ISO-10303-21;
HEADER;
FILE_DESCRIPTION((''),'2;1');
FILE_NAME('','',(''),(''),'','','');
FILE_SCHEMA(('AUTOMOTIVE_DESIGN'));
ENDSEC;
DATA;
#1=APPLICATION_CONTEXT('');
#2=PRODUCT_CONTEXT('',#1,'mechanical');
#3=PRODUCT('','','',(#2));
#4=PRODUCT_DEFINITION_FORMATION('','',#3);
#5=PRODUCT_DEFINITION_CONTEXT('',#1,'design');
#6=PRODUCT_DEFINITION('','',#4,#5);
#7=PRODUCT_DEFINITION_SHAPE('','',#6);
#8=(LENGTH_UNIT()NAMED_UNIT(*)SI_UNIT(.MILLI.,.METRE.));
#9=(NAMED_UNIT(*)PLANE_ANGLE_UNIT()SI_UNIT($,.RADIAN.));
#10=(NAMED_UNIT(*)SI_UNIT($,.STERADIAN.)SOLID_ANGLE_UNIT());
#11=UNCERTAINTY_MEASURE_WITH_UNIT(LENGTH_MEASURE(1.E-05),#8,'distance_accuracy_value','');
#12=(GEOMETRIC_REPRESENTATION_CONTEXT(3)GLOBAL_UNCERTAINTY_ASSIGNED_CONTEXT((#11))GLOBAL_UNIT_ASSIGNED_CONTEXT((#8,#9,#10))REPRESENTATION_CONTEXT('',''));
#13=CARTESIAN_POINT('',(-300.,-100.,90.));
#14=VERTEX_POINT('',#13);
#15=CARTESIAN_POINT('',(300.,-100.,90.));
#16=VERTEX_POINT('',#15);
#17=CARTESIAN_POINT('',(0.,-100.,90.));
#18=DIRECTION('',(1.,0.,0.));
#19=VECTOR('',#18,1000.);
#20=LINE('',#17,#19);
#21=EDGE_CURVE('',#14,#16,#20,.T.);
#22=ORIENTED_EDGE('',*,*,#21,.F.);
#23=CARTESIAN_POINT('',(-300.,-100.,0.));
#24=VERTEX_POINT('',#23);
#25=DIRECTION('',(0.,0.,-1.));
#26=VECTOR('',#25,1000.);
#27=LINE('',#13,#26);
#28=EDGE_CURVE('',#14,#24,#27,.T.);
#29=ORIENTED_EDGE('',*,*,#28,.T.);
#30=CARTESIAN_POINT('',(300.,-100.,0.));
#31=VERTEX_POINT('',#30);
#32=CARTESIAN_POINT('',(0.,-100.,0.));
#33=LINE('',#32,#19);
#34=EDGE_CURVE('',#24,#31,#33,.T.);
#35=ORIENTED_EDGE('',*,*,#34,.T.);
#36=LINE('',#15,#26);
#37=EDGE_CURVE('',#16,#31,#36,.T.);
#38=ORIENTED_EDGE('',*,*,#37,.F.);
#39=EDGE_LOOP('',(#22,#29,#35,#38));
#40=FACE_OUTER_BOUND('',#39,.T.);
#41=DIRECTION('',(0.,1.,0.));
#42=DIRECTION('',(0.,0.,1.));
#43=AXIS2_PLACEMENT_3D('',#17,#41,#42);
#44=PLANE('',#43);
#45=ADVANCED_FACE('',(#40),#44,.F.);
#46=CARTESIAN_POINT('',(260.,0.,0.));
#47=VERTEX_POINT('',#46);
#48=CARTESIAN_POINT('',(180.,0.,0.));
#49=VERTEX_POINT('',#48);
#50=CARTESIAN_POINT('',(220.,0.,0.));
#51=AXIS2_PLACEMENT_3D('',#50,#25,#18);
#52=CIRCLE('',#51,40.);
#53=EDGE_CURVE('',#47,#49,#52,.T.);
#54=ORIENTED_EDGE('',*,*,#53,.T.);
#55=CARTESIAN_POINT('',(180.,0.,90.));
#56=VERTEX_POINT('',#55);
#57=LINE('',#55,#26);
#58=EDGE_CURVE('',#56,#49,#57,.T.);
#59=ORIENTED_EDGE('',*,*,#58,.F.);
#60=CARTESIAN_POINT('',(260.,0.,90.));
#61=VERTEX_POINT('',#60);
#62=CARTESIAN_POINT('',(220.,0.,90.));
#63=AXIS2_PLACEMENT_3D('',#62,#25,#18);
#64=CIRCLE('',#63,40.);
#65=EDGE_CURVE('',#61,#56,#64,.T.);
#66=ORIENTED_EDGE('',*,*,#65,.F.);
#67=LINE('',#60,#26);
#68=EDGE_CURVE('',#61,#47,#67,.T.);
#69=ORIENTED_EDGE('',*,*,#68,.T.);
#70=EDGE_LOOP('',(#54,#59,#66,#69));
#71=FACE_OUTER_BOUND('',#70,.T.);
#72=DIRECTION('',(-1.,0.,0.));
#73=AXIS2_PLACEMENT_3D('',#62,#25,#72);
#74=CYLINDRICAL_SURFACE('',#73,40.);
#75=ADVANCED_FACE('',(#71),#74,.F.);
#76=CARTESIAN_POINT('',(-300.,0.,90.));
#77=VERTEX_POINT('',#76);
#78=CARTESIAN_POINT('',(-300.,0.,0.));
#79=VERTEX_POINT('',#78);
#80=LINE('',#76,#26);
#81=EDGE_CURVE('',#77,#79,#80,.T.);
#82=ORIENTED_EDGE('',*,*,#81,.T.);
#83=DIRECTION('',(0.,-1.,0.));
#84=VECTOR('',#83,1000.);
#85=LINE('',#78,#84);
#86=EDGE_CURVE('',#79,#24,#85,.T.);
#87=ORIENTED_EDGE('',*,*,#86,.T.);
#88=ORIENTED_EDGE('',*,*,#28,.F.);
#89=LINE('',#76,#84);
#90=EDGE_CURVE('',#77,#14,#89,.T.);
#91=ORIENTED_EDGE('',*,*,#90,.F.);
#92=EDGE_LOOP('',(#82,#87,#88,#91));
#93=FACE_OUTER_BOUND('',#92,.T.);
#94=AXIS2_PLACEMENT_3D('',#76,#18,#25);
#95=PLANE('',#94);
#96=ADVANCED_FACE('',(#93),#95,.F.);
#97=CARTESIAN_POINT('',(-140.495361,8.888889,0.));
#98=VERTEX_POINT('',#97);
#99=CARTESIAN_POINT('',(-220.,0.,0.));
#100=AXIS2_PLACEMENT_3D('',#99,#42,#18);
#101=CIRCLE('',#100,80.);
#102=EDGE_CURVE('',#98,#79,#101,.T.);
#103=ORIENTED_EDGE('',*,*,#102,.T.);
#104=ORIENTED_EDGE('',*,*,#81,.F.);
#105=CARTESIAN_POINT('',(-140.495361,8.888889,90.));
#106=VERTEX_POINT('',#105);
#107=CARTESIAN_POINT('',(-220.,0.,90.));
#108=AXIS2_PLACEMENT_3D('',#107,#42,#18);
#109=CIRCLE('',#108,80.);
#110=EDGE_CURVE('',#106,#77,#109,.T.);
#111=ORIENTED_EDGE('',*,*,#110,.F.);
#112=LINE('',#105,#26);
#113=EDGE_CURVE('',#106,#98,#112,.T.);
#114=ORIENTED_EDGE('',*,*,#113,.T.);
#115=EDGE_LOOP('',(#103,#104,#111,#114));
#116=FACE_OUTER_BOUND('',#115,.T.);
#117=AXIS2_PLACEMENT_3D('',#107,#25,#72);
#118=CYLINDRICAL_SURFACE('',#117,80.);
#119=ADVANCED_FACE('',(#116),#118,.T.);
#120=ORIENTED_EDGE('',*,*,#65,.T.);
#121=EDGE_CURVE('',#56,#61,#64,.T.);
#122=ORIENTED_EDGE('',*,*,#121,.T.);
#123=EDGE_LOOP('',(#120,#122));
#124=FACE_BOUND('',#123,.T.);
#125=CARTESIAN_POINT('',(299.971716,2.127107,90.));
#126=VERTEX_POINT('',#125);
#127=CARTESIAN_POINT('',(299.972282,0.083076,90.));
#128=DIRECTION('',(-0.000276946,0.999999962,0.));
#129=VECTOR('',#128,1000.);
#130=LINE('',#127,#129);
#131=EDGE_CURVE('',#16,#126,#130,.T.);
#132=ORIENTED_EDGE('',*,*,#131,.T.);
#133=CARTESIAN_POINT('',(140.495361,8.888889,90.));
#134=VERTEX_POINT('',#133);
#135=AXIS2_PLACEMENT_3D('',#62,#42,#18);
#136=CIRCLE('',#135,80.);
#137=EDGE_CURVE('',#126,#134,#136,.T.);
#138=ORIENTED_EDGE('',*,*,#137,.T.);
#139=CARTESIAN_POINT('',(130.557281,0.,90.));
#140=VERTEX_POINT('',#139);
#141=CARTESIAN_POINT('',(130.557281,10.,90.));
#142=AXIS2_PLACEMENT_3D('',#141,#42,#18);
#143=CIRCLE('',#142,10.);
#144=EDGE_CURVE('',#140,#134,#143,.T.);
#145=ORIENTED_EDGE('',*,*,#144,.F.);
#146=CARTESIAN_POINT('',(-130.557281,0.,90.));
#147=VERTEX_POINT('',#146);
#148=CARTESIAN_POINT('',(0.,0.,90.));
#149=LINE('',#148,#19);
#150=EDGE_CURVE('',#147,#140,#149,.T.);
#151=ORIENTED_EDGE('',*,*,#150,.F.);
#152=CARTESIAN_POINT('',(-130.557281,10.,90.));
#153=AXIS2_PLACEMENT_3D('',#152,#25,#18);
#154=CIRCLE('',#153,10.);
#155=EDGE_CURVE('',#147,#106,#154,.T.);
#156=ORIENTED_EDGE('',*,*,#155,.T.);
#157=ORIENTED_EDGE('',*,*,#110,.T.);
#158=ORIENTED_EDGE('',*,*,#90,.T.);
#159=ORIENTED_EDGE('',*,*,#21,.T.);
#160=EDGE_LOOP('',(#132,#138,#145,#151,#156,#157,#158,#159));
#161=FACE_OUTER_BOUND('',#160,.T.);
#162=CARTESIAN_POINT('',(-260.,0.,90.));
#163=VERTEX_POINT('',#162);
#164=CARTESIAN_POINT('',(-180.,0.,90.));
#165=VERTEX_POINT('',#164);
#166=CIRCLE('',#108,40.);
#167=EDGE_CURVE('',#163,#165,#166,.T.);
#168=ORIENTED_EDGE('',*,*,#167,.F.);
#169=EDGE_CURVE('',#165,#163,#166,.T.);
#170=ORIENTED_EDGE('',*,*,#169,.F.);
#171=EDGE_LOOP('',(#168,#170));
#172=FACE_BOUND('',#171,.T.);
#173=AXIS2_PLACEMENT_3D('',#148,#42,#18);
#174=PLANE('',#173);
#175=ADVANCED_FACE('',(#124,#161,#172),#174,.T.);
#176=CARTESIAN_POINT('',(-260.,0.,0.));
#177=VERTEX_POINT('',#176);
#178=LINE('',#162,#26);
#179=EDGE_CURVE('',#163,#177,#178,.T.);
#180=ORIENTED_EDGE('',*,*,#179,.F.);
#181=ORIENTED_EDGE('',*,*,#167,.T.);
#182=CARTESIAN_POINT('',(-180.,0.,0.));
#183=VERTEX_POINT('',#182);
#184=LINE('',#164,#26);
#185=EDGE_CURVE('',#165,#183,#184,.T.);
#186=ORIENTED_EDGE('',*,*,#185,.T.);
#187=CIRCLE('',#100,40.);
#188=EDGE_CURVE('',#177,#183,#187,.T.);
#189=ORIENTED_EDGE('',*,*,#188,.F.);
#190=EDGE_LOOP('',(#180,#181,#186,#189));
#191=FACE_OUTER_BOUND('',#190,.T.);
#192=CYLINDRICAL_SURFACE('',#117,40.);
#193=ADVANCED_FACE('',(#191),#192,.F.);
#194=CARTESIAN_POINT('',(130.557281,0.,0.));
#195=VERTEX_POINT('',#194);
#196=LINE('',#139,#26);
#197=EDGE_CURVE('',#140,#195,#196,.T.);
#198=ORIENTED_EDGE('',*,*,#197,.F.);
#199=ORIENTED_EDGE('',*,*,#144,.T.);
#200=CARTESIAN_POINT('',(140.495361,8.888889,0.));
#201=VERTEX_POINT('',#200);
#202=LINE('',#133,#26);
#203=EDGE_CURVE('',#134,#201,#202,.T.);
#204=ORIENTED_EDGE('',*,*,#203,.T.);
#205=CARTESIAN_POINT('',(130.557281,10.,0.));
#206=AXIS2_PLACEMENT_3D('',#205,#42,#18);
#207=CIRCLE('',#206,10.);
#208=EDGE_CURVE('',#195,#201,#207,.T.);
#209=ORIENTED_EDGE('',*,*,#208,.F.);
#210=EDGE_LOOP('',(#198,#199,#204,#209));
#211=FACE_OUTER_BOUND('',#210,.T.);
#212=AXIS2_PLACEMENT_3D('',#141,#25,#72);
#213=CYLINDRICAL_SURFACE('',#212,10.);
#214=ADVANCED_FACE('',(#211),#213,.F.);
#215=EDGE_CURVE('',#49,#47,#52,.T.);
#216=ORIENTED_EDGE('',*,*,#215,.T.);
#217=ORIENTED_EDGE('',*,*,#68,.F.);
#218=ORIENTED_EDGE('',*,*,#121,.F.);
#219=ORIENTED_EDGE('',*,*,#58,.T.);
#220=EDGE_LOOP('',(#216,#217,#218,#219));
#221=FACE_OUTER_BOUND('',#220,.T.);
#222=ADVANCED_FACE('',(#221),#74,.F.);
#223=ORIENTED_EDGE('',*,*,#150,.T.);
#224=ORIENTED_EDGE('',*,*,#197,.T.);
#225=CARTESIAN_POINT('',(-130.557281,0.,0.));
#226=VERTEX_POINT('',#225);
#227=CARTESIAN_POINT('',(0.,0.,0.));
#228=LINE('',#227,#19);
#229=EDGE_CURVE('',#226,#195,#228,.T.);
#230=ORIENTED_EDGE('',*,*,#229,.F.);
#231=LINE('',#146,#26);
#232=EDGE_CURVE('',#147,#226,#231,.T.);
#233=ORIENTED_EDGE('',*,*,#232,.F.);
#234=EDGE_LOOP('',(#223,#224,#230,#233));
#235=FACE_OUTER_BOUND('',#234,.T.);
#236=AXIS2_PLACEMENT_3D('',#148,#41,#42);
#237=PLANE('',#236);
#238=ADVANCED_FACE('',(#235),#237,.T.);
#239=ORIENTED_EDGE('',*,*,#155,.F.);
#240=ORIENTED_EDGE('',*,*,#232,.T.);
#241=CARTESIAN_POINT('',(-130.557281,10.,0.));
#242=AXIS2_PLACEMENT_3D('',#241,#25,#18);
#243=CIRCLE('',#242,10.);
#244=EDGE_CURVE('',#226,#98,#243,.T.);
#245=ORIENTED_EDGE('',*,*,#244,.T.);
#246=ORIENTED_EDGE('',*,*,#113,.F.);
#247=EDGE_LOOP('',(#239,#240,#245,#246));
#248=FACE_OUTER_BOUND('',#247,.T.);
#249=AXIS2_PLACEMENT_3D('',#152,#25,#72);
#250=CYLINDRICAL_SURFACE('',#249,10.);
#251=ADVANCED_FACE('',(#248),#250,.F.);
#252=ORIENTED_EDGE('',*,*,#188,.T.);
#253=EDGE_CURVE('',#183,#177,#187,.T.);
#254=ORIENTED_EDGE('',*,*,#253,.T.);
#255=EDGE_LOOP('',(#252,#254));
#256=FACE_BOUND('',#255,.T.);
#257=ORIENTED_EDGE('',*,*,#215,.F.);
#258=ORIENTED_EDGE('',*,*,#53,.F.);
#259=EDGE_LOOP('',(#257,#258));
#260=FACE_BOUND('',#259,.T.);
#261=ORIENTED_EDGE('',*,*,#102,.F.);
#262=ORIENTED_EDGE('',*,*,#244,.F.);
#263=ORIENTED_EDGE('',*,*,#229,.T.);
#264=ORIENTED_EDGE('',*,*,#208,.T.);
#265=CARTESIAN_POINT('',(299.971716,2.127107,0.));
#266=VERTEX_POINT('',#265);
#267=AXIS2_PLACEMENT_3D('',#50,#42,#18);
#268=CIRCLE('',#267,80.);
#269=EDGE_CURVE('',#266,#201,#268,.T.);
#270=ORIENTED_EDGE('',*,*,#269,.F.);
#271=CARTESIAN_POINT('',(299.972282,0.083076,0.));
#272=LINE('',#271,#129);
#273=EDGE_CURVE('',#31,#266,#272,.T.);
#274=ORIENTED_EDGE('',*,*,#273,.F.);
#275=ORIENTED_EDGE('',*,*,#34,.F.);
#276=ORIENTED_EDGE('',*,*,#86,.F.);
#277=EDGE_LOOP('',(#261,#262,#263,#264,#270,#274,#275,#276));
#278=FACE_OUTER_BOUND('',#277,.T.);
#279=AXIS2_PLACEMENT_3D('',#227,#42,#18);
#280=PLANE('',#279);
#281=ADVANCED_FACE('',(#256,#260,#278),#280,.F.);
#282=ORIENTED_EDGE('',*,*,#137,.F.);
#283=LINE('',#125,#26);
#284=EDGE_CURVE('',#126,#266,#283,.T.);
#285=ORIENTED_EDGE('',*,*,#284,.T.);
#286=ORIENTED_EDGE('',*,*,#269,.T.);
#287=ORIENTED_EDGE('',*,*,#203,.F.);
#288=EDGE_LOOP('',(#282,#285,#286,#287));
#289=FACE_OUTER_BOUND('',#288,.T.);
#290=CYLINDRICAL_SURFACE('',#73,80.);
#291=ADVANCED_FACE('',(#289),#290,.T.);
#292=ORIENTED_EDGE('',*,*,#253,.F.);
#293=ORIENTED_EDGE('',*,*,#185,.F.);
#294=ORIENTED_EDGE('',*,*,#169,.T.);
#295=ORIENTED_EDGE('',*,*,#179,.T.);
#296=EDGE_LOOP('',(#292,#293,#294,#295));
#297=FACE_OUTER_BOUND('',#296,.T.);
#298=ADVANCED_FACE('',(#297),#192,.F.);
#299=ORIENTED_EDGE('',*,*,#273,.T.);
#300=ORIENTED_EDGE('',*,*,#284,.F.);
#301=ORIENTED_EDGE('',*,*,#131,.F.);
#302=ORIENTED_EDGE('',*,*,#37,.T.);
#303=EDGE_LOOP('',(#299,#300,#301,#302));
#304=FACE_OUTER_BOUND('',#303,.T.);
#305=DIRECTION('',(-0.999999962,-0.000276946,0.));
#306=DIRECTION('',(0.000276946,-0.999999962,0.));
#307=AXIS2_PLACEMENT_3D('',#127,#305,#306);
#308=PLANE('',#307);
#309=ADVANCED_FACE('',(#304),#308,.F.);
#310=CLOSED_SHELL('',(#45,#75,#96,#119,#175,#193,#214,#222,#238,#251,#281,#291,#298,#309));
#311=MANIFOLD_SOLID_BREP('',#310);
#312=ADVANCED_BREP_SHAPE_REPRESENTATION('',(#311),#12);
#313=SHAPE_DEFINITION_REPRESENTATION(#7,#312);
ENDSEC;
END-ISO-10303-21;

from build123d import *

# Parameters (mm, degrees)
SKETCH1_R           = 40
BOSS_EXTRUDE2_DEPTH = 90


with BuildPart() as part:
    # Sketch1 → Boss-Extrude2 (new body)
    with BuildSketch(Plane.XY):
        with BuildLine():
            ThreePointArc((-140.4953608, 8.888888889), (-224.451340472, 79.876063799), (-300, 0))
            Line((-300, 0), (-300, -100))
            Line((-300, -100), (300, -100))
            Line((300, -100), (299.972882257, -2.08281146))
            Line((299.972882257, -2.08281146), (299.971716338, 2.127107427))
            ThreePointArc((299.971716338, 2.127107427), (223.388947093, 79.928186753), (140.4953608, 8.888888889))
            ThreePointArc((140.4953608, 8.888888889), (137.223947567, 2.546440075), (130.5572809, 0))
            Line((130.5572809, 0), (-130.5572809, 0))
            ThreePointArc((-130.5572809, 0), (-137.223947567, 2.546440075), (-140.4953608, 8.888888889))
        make_face()
        with Locations(Location((-220, 0, 0), (0, 0, 180))):
            Circle(SKETCH1_R, mode=Mode.SUBTRACT)
        with Locations(Location((220, 0, 0), (0, 0, 180))):
            Circle(SKETCH1_R, mode=Mode.SUBTRACT)
    extrude(amount=BOSS_EXTRUDE2_DEPTH)


solid = part.part
